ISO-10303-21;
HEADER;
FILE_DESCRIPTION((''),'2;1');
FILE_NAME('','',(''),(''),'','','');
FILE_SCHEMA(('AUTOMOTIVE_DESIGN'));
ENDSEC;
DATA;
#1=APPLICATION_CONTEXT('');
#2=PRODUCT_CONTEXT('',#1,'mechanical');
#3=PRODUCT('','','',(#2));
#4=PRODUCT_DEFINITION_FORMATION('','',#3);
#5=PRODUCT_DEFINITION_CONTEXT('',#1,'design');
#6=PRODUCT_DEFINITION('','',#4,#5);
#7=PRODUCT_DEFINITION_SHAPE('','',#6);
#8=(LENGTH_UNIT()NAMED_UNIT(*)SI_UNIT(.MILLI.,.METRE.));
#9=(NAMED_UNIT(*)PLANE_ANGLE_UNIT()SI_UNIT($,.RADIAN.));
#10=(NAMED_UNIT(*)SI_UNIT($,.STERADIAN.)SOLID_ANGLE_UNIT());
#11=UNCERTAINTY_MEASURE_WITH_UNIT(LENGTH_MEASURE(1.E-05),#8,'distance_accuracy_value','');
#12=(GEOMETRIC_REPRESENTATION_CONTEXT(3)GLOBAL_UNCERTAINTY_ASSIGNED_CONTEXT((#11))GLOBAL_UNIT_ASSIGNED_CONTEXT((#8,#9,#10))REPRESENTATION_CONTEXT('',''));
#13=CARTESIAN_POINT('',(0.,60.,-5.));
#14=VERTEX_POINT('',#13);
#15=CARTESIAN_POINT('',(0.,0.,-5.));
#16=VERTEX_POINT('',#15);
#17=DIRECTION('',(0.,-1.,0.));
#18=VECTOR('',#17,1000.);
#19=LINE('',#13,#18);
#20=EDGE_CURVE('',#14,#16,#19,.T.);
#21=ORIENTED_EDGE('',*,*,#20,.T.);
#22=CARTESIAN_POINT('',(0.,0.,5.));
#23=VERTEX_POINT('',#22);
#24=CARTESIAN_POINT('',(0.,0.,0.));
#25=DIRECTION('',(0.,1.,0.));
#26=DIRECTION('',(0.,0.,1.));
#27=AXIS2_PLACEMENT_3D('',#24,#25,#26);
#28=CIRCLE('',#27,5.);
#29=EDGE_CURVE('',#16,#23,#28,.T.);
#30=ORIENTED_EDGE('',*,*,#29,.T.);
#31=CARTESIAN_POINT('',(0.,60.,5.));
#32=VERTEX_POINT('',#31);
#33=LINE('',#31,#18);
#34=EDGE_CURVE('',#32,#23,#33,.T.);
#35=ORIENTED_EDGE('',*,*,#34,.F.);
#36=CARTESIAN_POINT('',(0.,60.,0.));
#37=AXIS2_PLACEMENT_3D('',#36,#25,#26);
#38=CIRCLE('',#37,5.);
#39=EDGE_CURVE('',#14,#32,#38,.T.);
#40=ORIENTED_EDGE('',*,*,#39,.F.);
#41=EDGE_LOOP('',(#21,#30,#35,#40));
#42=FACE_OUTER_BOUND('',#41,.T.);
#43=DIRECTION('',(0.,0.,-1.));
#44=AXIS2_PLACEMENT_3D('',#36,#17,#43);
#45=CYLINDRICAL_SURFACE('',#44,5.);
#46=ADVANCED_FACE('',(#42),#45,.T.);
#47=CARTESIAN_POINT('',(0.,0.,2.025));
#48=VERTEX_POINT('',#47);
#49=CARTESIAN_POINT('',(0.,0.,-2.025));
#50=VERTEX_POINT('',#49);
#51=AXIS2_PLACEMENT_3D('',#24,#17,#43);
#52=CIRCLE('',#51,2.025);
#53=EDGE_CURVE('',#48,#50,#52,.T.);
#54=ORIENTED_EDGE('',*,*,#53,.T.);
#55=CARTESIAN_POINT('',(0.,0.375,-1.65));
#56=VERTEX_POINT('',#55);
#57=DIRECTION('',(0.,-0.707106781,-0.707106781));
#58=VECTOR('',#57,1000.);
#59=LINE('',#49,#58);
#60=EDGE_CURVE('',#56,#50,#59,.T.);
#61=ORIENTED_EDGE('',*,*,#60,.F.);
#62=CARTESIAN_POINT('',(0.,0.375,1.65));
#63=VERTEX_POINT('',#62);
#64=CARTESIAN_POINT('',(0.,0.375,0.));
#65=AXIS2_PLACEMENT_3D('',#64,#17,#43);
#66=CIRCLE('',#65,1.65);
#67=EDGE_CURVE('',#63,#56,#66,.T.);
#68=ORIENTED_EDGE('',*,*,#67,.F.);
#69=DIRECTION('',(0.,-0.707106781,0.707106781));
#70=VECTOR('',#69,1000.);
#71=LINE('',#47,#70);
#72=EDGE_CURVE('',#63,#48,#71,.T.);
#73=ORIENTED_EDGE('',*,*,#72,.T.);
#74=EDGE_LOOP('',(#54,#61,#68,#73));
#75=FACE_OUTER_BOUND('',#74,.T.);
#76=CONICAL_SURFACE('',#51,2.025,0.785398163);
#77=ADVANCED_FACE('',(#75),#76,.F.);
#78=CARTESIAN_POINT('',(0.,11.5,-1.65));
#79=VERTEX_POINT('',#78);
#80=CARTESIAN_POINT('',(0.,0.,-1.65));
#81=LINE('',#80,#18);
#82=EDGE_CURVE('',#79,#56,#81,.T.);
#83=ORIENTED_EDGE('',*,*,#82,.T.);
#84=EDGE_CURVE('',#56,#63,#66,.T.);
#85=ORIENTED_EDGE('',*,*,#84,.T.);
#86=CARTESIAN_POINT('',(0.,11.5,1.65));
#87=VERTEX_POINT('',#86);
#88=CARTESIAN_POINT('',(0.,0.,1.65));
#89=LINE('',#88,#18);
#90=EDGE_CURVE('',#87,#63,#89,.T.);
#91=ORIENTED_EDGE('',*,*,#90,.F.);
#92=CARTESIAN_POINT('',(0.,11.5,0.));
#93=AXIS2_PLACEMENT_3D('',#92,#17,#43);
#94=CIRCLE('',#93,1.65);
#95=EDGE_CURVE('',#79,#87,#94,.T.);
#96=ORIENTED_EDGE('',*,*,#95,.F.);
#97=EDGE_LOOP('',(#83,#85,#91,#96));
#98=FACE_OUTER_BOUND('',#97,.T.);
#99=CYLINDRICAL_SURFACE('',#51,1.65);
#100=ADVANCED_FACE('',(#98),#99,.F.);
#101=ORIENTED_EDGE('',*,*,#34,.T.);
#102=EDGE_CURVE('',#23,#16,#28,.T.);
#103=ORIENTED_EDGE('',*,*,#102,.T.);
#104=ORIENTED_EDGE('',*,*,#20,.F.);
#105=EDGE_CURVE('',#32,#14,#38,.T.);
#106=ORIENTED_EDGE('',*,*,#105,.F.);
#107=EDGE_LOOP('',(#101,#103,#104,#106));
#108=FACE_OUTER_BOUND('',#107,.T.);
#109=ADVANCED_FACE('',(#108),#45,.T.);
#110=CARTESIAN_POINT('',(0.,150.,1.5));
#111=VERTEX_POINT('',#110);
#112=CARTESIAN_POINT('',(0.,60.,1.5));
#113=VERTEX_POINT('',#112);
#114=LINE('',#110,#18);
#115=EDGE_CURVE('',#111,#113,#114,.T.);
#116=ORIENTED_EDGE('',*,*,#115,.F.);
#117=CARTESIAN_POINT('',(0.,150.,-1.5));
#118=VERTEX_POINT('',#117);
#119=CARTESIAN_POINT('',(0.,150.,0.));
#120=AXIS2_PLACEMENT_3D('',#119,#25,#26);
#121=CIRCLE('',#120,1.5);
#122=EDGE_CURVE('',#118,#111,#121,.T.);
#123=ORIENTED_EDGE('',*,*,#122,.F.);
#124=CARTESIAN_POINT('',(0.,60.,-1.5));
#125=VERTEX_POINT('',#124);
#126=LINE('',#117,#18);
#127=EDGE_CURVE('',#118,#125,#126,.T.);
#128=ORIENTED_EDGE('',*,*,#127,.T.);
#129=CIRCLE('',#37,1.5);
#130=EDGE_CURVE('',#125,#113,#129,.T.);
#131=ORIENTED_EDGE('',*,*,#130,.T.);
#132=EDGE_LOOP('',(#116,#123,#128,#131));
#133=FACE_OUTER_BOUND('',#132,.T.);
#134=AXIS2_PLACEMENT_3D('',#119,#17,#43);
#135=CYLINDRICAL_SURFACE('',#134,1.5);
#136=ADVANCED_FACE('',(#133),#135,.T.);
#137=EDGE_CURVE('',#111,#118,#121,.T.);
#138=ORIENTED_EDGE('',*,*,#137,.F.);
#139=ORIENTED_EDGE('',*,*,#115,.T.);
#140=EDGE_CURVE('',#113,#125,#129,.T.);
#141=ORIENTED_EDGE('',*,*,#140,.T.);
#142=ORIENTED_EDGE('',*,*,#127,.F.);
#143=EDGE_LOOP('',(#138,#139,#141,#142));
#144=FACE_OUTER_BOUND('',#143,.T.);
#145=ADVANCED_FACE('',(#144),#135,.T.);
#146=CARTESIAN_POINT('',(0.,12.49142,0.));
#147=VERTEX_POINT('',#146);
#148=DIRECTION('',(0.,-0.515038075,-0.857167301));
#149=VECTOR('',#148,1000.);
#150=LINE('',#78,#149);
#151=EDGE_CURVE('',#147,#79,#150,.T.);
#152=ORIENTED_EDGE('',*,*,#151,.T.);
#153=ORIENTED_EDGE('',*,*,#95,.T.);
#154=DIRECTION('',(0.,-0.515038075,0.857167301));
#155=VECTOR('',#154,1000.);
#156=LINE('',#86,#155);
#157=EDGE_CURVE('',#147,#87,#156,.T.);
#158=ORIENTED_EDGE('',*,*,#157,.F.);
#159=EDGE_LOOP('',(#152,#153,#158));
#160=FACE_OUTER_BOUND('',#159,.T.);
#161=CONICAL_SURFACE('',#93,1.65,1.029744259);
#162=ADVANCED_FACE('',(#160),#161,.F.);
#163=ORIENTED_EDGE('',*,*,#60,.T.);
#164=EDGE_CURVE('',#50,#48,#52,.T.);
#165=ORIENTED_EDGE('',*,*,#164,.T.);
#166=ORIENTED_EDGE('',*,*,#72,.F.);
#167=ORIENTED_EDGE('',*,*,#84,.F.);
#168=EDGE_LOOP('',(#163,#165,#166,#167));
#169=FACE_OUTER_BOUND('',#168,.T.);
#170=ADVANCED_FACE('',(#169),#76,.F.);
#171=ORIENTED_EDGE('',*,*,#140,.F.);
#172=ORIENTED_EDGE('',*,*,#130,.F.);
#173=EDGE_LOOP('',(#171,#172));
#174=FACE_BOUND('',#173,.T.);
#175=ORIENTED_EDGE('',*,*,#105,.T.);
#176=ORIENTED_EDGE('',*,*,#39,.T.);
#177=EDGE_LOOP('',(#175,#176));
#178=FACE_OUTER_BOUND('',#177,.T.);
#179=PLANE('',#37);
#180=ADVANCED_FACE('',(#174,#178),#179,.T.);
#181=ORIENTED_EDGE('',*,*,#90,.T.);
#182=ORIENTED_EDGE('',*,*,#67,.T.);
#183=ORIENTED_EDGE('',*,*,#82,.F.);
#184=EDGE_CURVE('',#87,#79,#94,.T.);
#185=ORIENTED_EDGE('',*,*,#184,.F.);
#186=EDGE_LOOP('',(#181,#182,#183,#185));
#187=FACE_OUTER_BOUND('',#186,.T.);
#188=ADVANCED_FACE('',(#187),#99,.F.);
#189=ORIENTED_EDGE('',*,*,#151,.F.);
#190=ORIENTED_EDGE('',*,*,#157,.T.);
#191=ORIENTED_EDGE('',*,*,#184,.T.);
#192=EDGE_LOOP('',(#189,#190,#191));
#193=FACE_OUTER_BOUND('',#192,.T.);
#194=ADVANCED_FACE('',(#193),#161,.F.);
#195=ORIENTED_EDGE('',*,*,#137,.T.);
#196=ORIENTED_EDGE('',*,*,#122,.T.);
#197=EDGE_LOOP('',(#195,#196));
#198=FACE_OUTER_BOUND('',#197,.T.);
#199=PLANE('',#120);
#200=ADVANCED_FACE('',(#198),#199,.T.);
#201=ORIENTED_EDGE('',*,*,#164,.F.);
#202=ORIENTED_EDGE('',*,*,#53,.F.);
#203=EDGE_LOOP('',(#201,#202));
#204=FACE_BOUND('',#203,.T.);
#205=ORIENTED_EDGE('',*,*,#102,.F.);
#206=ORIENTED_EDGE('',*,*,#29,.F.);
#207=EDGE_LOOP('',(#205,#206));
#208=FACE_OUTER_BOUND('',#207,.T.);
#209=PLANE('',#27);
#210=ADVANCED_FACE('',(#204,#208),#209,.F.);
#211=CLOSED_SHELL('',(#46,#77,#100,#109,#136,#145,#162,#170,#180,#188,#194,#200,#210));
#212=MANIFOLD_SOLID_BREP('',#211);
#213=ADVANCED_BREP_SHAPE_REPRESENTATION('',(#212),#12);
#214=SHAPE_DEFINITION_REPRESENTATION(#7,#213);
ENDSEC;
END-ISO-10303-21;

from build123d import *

# Parameters (mm, degrees)
SKETCH1_R                   = 5
BOSS_EXTRUDE1_DEPTH         = 60
SKETCH2_R                   = 1.5
BOSS_EXTRUDE2_DEPTH         = 90
M4_TAPPED_HOLE1_D           = 3.3
M4_TAPPED_HOLE1_DEPTH       = 11.5
M4_TAPPED_HOLE1_CSINK_D     = 4.05
M4_TAPPED_HOLE1_CSINK_ANGLE = 90
M4_TAPPED_HOLE1_TIP         = 0.991420021


with BuildPart() as part:
    # Sketch1 → Boss-Extrude1 (new body)
    with BuildSketch(Plane(origin=(0, 0, 0), x_dir=(1, 0, 0), z_dir=(0, 1, 0))):
        with Locations(Location((0, 0, 0), (0, 0, 270))):
            Circle(SKETCH1_R)
    extrude(amount=BOSS_EXTRUDE1_DEPTH)

    # Sketch2 → Boss-Extrude2 (add)
    with BuildSketch(Plane(origin=(0, 60, 0), x_dir=(1, 0, 0), z_dir=(0, 1, 0))):
        with Locations(Location((0, 0, 0), (0, 0, 90))):
            Circle(SKETCH2_R)
    extrude(amount=BOSS_EXTRUDE2_DEPTH)

    # M4 Tapped Hole1
    with Locations(Plane(origin=(0, 0, 0), x_dir=(-1, 0, 0), z_dir=(0, -1, 0))):
        with Locations((0, 0)):
            CounterSinkHole(M4_TAPPED_HOLE1_D / 2, M4_TAPPED_HOLE1_CSINK_D / 2, depth=M4_TAPPED_HOLE1_DEPTH, counter_sink_angle=M4_TAPPED_HOLE1_CSINK_ANGLE)
            with Locations((0, 0, -(M4_TAPPED_HOLE1_DEPTH + M4_TAPPED_HOLE1_TIP / 2))):  # 118° drill point
                Cone(0, M4_TAPPED_HOLE1_D / 2, M4_TAPPED_HOLE1_TIP, mode=Mode.SUBTRACT)


solid = part.part
